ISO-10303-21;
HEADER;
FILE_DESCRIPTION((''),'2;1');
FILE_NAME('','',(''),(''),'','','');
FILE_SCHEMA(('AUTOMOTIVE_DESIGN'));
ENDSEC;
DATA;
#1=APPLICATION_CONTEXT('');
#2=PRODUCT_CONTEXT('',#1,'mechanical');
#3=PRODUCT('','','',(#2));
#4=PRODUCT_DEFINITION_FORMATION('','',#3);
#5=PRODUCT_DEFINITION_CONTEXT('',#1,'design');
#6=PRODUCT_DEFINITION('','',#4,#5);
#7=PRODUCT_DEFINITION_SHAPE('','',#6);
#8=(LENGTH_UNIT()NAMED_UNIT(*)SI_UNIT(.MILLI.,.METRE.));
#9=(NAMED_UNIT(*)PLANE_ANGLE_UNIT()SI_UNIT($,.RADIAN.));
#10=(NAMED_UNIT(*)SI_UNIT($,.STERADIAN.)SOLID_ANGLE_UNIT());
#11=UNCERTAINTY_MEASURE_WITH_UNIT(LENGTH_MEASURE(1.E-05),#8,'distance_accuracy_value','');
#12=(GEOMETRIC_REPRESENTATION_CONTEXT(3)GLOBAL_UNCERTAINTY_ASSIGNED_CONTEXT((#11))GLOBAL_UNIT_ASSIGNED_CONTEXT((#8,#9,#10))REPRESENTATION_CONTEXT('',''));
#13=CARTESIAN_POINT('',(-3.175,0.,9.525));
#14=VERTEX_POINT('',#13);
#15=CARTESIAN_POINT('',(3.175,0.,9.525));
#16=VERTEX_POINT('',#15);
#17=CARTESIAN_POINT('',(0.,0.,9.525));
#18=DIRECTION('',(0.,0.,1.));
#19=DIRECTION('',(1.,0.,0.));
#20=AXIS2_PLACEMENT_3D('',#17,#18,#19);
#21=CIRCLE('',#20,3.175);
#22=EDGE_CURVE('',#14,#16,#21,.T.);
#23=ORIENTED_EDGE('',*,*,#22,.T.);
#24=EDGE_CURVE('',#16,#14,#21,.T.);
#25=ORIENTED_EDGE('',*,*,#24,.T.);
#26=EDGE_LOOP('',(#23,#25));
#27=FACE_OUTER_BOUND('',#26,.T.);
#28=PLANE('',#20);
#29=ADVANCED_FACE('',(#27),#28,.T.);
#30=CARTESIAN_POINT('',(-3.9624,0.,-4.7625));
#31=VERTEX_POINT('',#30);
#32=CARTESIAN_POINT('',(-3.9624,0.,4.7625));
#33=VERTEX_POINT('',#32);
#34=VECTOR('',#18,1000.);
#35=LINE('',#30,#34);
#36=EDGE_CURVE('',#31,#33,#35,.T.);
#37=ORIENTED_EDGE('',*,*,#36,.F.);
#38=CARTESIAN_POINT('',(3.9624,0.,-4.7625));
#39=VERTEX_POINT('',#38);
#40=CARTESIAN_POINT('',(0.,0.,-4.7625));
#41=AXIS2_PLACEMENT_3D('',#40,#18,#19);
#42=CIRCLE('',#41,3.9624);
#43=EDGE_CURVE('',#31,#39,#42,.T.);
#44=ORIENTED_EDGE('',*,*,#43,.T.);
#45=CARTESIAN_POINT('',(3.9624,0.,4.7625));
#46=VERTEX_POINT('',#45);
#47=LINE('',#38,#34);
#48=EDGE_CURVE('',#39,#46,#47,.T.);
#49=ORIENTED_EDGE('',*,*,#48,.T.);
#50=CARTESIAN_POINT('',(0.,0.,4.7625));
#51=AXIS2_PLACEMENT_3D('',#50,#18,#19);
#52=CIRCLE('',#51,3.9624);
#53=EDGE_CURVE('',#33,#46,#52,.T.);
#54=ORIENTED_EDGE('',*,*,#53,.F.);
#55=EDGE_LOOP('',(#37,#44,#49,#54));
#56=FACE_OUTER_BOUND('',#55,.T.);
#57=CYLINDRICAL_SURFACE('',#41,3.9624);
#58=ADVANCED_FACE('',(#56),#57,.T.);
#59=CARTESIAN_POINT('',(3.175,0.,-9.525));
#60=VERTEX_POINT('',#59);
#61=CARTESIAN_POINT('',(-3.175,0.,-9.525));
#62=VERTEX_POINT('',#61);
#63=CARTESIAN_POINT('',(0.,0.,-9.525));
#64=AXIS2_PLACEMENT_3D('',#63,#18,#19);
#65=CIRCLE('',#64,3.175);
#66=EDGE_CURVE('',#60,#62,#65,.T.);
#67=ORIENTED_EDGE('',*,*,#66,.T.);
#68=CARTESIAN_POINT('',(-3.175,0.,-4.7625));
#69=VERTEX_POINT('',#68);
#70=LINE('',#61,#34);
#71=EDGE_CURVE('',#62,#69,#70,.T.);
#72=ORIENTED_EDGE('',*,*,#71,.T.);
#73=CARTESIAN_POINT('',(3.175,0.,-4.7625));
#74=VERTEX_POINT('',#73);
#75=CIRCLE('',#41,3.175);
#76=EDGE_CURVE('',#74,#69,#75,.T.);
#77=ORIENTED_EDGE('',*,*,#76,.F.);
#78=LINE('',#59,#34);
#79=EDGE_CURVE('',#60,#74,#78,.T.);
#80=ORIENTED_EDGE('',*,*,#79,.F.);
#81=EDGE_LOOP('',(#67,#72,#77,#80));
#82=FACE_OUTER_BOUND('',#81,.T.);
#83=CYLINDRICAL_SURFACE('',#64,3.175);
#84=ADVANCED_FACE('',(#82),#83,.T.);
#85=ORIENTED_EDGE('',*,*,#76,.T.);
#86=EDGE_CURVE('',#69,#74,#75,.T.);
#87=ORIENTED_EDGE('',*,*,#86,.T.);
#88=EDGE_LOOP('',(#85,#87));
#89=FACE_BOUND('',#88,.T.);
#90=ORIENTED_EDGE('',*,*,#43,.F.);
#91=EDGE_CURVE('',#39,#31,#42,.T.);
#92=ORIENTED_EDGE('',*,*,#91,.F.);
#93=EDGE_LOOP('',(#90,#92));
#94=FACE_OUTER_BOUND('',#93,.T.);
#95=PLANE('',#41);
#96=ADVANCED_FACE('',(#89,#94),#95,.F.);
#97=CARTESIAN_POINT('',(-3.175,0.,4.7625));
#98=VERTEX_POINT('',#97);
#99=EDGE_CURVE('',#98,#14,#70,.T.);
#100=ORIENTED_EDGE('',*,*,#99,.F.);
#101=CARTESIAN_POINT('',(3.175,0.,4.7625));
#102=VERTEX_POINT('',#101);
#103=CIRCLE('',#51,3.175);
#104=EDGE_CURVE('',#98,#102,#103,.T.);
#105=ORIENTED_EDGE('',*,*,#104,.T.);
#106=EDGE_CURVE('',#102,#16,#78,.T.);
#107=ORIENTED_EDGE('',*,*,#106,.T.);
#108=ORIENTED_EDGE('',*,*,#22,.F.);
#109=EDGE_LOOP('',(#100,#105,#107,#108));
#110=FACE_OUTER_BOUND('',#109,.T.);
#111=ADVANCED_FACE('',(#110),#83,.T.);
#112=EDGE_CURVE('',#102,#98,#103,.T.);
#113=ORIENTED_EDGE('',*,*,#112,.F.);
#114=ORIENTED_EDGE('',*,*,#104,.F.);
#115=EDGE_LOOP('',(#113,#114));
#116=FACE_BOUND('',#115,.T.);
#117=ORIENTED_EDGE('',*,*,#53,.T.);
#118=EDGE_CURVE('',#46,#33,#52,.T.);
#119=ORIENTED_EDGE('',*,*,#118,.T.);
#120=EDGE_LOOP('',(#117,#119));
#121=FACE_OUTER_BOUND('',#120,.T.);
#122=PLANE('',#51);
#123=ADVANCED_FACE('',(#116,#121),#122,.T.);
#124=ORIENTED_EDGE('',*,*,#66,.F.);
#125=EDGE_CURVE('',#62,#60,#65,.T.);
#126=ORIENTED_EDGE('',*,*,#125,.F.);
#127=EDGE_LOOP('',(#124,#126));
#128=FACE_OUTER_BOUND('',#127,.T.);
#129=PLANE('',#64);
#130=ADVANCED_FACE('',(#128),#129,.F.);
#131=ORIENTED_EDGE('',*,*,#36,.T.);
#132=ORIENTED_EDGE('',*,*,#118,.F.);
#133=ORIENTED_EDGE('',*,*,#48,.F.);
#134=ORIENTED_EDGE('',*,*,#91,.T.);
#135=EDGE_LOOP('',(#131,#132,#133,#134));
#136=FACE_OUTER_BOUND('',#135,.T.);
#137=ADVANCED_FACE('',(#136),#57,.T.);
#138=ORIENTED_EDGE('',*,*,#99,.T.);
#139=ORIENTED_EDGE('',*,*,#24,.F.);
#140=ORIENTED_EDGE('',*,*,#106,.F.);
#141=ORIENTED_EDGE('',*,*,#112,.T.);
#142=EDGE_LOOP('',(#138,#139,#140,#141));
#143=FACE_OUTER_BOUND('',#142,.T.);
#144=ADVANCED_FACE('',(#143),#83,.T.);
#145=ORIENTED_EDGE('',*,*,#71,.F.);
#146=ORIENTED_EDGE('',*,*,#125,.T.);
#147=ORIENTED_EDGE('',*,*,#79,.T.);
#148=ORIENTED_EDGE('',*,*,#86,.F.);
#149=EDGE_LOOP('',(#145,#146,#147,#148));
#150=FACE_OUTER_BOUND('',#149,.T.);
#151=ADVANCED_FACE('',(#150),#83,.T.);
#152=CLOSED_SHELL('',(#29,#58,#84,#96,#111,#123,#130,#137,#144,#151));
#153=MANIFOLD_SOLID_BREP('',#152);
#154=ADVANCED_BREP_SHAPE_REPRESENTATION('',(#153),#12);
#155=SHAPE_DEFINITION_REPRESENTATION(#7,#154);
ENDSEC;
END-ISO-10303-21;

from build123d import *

# Parameters (mm, degrees)
BOSS_EXTRUDE1_DEPTH      = 4.7625
BOSS_EXTRUDE1_DEPTH_BACK = 4.7625
SKETCH1_R                = 3.9624
BOSS_EXTRUDE2_DEPTH      = 9.525
BOSS_EXTRUDE2_DEPTH_BACK = 9.525
BOSS_EXTRUDE2_START      = -4.7625
SKETCH2_R                = 3.175


with BuildPart() as part:
    # Sketch1 → Boss-Extrude1 (new, two sides: drawn at the far end of the back side and taken through both)
    with BuildSketch(Plane.XY.offset(-BOSS_EXTRUDE1_DEPTH_BACK)):
        Circle(SKETCH1_R)
    extrude(amount=BOSS_EXTRUDE1_DEPTH + BOSS_EXTRUDE1_DEPTH_BACK)

    # Sketch2 → Boss-Extrude2 (add, two sides: drawn at the far end of the back side and taken through both)
    with BuildSketch(Plane.XY.offset(4.7625).offset(BOSS_EXTRUDE2_START - BOSS_EXTRUDE2_DEPTH_BACK)):
        Circle(SKETCH2_R)
    extrude(amount=BOSS_EXTRUDE2_DEPTH + BOSS_EXTRUDE2_DEPTH_BACK)


solid = part.part
